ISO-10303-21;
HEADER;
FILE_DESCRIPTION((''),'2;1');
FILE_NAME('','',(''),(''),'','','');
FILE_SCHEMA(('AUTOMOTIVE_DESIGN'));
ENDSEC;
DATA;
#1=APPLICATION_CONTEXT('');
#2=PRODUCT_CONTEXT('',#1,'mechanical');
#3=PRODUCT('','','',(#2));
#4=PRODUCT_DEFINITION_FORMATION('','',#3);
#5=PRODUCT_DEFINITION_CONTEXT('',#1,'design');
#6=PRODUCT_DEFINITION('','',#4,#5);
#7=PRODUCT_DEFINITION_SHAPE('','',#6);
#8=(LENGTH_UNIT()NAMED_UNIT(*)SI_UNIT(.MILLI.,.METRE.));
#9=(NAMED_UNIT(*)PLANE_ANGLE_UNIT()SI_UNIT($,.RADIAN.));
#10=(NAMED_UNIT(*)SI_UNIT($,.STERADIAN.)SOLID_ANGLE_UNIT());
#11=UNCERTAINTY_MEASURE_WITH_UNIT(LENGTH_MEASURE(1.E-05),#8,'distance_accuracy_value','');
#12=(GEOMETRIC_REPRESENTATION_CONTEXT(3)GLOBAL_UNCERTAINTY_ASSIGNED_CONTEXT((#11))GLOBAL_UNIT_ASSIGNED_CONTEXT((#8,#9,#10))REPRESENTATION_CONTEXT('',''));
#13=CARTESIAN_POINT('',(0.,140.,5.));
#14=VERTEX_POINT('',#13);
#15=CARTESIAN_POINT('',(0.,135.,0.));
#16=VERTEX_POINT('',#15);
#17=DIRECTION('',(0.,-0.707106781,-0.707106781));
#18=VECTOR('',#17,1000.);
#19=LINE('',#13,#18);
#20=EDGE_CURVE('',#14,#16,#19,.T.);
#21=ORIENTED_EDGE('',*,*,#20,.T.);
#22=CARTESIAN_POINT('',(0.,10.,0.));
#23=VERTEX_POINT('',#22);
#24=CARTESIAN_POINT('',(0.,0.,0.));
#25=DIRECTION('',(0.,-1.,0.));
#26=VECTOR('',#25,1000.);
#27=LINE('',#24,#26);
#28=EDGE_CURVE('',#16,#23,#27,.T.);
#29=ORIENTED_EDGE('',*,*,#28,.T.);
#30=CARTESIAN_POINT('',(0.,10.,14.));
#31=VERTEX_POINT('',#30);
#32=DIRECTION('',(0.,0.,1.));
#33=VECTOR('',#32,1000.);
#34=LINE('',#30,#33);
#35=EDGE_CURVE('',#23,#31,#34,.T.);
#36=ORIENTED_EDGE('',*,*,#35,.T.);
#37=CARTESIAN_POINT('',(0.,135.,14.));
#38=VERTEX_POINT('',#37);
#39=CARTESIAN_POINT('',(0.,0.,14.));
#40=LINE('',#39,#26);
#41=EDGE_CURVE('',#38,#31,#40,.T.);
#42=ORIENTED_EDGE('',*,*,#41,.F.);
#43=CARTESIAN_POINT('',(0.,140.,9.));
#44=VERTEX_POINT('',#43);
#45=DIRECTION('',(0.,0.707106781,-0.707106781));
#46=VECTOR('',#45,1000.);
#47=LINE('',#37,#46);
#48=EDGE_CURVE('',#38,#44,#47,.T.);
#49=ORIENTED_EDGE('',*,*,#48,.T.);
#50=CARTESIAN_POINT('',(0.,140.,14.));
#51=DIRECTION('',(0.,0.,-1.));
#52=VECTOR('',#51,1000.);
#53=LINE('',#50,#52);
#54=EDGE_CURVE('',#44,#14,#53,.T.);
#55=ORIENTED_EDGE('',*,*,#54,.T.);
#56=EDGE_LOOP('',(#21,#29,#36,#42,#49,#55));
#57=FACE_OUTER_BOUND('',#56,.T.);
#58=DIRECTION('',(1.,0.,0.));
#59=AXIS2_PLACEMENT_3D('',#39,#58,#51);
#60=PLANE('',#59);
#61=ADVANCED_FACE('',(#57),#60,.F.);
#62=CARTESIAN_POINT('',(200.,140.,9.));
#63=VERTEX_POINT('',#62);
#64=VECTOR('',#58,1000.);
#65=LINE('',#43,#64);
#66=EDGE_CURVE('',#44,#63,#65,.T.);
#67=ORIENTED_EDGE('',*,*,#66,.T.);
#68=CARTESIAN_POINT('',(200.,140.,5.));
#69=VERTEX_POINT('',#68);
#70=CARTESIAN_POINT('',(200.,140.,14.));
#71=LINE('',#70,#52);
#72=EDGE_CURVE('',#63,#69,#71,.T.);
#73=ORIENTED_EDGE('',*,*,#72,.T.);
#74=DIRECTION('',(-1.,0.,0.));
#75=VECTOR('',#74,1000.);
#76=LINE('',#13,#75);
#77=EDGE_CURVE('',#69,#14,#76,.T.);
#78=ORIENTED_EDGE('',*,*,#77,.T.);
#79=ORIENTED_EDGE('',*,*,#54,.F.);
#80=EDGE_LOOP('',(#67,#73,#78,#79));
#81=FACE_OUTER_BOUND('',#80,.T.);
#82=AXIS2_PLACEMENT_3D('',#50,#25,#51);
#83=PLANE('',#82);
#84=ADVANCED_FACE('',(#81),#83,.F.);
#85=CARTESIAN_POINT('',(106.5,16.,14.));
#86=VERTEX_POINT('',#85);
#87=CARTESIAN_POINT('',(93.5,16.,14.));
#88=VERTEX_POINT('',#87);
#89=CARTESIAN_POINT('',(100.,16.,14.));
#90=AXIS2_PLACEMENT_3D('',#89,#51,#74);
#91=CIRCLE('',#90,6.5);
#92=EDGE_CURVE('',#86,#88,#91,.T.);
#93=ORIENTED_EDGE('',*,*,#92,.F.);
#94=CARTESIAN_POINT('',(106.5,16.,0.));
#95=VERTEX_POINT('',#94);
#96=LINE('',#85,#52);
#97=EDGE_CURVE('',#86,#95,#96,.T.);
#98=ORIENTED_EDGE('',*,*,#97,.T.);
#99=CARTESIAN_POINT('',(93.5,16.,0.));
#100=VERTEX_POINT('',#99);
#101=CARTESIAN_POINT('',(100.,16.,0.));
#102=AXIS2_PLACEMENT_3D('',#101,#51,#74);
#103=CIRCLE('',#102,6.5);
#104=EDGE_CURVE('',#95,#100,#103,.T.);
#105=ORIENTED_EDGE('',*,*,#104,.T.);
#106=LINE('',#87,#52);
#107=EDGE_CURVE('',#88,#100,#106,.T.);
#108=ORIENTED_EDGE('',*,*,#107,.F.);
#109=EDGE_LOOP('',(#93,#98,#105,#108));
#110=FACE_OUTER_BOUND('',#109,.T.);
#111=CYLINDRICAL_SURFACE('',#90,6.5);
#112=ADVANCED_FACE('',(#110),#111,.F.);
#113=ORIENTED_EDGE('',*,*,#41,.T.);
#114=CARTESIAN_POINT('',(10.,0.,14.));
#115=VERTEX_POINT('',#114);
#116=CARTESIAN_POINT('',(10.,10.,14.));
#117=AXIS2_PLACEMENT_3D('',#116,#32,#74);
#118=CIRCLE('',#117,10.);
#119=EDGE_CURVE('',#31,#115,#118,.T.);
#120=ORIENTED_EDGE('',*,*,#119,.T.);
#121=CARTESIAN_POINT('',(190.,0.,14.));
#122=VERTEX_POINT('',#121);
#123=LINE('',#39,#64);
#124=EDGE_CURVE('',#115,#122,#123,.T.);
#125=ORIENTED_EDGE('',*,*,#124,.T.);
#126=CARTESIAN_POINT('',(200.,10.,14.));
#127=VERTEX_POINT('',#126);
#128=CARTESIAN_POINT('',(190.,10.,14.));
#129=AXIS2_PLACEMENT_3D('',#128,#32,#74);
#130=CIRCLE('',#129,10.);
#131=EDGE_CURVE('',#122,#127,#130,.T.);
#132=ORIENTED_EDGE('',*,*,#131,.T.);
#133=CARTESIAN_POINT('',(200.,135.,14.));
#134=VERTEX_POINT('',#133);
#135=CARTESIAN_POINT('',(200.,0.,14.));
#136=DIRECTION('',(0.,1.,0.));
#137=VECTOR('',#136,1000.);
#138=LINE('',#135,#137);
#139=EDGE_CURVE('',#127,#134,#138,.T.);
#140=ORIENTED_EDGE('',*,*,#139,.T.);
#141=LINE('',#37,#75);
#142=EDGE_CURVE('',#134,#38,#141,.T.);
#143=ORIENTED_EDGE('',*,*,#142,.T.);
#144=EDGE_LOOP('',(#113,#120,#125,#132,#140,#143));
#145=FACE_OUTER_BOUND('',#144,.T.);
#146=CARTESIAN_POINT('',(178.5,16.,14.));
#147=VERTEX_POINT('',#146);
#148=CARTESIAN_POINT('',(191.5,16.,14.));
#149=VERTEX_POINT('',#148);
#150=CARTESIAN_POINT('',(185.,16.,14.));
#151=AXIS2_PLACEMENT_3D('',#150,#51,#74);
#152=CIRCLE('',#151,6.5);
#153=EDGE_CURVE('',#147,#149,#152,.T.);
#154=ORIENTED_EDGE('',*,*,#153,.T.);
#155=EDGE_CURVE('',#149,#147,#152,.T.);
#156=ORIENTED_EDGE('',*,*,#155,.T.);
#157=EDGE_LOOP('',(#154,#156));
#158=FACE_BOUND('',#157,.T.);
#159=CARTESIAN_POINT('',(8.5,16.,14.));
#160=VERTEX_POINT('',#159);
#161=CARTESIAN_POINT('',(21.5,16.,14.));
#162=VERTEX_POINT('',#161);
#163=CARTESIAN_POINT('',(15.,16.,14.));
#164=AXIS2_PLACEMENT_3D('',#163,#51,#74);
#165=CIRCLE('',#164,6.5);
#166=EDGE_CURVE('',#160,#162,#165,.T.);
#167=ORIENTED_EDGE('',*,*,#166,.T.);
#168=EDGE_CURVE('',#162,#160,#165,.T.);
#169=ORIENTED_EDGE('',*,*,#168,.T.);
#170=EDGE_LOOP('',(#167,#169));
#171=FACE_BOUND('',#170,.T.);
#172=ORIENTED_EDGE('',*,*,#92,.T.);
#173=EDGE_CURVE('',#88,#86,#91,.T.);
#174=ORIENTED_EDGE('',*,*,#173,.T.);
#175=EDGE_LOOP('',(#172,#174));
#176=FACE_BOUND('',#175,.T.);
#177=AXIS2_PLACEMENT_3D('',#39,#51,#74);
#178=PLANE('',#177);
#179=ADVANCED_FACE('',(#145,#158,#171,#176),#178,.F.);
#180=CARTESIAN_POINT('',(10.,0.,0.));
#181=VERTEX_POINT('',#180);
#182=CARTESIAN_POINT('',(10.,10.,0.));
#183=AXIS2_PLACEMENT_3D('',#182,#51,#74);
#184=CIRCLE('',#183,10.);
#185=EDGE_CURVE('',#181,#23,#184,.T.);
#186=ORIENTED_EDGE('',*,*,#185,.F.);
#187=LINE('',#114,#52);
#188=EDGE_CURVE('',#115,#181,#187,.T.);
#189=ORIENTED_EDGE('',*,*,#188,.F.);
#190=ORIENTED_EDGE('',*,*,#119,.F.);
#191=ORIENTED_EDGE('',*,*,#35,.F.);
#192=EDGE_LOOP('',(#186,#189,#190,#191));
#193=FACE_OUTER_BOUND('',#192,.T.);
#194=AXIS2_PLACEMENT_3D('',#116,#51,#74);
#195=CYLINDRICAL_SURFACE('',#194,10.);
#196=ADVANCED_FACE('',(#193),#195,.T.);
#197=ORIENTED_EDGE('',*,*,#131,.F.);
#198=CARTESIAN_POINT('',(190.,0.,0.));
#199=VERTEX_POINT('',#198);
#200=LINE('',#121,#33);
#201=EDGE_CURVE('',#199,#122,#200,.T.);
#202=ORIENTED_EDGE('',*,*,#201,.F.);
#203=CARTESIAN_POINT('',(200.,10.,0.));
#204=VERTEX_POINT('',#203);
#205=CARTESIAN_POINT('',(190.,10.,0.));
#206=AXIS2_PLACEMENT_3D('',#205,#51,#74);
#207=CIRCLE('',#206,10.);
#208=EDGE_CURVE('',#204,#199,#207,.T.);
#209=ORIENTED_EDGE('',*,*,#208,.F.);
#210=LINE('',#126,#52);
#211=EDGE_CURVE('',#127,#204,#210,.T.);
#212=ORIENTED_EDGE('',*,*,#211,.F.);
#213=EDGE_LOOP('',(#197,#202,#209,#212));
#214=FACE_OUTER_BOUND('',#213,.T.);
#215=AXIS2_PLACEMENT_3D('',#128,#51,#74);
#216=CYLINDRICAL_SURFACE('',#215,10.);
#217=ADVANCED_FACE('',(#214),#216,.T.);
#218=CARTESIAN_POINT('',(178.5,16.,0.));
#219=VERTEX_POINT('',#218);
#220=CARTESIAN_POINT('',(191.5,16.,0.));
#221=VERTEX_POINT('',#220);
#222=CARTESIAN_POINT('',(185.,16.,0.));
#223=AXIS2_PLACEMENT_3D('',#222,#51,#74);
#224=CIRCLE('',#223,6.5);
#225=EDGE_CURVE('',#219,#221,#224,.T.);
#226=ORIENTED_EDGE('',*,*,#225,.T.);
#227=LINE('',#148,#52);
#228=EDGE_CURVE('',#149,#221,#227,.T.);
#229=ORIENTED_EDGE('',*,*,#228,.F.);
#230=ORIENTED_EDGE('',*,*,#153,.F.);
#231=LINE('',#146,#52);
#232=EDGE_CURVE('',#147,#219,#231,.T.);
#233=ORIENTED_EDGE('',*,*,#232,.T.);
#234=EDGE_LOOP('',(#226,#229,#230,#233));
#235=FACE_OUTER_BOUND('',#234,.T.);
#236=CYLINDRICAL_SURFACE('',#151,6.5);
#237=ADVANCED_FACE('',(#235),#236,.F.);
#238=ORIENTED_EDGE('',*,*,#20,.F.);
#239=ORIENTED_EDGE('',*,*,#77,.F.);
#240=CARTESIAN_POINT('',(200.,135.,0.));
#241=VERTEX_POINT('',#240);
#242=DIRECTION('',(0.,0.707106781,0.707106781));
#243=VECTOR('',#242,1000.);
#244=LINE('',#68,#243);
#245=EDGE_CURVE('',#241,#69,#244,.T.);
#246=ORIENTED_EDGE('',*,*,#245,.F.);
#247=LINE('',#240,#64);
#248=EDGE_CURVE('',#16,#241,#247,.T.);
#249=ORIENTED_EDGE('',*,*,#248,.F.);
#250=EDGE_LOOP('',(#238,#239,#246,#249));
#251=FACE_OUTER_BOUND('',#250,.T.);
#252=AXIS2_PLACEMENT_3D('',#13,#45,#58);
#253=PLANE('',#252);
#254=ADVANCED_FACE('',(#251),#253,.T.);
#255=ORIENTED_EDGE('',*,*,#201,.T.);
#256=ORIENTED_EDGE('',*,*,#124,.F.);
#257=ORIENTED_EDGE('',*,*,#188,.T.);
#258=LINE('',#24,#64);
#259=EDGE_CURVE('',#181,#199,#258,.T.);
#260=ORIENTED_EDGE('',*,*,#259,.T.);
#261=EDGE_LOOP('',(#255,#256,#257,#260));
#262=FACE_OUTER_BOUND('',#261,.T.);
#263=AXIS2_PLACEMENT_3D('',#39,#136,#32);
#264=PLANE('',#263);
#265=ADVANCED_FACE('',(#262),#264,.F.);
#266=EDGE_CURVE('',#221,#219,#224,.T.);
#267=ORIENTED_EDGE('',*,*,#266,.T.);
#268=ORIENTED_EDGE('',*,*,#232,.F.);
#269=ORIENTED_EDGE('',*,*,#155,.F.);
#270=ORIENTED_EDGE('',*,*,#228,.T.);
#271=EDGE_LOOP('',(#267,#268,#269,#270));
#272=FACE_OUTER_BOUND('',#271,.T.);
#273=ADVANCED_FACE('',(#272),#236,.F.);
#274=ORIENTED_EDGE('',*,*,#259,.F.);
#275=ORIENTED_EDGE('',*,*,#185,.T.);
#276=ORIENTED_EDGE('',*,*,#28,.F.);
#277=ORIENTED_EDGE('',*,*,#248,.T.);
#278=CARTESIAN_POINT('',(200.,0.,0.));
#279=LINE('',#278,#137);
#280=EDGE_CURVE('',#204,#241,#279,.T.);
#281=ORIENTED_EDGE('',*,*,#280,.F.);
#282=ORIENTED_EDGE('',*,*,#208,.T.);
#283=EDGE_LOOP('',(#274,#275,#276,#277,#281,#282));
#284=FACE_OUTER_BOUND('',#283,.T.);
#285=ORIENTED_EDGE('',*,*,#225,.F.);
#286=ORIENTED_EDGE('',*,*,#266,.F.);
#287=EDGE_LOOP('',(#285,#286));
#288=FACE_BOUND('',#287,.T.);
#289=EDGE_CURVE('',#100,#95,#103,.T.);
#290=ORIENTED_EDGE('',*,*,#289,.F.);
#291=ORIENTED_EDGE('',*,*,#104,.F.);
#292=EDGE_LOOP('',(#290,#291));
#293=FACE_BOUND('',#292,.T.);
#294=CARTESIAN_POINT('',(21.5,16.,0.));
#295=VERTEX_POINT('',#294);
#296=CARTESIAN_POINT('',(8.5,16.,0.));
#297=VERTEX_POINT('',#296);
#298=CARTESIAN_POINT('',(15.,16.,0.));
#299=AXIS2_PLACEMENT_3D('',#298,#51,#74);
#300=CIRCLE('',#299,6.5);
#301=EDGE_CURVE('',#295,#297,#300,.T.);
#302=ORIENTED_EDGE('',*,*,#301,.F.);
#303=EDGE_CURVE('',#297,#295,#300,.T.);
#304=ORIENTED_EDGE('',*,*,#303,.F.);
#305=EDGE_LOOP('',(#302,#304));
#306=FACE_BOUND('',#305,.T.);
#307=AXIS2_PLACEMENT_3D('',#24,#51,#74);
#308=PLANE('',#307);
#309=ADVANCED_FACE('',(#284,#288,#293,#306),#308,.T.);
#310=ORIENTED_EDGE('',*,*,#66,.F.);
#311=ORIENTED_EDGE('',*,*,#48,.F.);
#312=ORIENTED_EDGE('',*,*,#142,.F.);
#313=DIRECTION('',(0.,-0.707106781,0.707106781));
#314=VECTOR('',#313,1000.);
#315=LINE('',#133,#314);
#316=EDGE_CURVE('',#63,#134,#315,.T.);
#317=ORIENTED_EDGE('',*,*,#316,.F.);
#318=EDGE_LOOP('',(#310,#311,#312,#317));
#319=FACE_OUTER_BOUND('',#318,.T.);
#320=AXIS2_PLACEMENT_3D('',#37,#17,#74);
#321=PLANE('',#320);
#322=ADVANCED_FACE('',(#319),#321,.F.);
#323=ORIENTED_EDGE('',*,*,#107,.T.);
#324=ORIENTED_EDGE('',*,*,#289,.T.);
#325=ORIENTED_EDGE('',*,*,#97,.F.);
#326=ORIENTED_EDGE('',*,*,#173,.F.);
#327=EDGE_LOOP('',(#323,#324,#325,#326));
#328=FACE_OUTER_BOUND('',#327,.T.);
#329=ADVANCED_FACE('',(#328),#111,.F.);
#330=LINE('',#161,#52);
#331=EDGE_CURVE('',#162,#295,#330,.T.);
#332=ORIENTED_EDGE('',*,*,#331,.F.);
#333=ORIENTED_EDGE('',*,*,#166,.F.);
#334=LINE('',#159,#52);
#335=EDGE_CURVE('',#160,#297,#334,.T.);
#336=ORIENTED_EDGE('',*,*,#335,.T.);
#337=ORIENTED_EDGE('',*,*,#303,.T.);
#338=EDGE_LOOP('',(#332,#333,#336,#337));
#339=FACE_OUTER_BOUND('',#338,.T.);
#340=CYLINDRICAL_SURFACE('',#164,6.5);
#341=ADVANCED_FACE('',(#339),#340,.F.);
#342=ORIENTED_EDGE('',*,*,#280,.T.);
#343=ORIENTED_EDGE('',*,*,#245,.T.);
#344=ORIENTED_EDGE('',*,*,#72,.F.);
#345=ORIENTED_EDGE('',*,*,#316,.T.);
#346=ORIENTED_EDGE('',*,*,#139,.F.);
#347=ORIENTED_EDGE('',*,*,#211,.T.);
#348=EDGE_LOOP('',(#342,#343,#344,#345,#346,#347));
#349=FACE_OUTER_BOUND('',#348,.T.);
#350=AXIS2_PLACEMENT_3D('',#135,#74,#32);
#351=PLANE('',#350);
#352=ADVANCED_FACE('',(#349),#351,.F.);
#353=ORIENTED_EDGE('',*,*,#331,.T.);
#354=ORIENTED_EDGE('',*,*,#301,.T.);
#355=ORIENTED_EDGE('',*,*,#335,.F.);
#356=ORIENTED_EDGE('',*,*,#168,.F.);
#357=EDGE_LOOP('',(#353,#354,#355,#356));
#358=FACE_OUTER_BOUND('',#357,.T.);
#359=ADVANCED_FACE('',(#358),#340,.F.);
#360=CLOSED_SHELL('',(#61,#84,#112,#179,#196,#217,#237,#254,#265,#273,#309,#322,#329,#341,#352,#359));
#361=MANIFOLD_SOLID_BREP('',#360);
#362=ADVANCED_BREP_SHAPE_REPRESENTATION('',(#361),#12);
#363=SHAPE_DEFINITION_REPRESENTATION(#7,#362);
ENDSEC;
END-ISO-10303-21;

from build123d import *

# Parameters (mm, degrees)
SKETCH1_W           = 200
SKETCH1_H           = 140
BOSS_EXTRUDE1_DEPTH = 14
CHAMFER1_SIZE       = 5
SKETCH3_R           = 6.5
CUT_EXTRUDE2_DEPTH  = 245.532206468
FILLET1_R           = 10


with BuildPart() as part:
    # Sketch1 → Boss-Extrude1 (new body)
    with BuildSketch(Plane.XY):
        with Locations((100, 70)):
            Rectangle(SKETCH1_W, SKETCH1_H)
    extrude(amount=BOSS_EXTRUDE1_DEPTH)

    # Chamfer1
    chamfer1_edges = [part.edges().sort_by_distance(p)[0] for p in [
        (100, 140, 14),
        (100, 140, 0),
    ]]
    chamfer(chamfer1_edges, length=CHAMFER1_SIZE)

    # Sketch3 → Cut-Extrude2 (cut, through all)
    with BuildSketch(Plane(origin=(0, 0, 0), x_dir=(-1, 0, 0), z_dir=(0, 0, -1))):
        with Locations((-185, 16)):
            Circle(SKETCH3_R)
        with Locations((-100, 16)):
            Circle(SKETCH3_R)
        with Locations((-15, 16)):
            Circle(SKETCH3_R)
    extrude(amount=-CUT_EXTRUDE2_DEPTH, mode=Mode.SUBTRACT)

    # Fillet1
    fillet1_edges = [part.edges().sort_by_distance(p)[0] for p in [
        (200, 0, 7),
        (0, 0, 7),
    ]]
    fillet(fillet1_edges, radius=FILLET1_R)


solid = part.part
